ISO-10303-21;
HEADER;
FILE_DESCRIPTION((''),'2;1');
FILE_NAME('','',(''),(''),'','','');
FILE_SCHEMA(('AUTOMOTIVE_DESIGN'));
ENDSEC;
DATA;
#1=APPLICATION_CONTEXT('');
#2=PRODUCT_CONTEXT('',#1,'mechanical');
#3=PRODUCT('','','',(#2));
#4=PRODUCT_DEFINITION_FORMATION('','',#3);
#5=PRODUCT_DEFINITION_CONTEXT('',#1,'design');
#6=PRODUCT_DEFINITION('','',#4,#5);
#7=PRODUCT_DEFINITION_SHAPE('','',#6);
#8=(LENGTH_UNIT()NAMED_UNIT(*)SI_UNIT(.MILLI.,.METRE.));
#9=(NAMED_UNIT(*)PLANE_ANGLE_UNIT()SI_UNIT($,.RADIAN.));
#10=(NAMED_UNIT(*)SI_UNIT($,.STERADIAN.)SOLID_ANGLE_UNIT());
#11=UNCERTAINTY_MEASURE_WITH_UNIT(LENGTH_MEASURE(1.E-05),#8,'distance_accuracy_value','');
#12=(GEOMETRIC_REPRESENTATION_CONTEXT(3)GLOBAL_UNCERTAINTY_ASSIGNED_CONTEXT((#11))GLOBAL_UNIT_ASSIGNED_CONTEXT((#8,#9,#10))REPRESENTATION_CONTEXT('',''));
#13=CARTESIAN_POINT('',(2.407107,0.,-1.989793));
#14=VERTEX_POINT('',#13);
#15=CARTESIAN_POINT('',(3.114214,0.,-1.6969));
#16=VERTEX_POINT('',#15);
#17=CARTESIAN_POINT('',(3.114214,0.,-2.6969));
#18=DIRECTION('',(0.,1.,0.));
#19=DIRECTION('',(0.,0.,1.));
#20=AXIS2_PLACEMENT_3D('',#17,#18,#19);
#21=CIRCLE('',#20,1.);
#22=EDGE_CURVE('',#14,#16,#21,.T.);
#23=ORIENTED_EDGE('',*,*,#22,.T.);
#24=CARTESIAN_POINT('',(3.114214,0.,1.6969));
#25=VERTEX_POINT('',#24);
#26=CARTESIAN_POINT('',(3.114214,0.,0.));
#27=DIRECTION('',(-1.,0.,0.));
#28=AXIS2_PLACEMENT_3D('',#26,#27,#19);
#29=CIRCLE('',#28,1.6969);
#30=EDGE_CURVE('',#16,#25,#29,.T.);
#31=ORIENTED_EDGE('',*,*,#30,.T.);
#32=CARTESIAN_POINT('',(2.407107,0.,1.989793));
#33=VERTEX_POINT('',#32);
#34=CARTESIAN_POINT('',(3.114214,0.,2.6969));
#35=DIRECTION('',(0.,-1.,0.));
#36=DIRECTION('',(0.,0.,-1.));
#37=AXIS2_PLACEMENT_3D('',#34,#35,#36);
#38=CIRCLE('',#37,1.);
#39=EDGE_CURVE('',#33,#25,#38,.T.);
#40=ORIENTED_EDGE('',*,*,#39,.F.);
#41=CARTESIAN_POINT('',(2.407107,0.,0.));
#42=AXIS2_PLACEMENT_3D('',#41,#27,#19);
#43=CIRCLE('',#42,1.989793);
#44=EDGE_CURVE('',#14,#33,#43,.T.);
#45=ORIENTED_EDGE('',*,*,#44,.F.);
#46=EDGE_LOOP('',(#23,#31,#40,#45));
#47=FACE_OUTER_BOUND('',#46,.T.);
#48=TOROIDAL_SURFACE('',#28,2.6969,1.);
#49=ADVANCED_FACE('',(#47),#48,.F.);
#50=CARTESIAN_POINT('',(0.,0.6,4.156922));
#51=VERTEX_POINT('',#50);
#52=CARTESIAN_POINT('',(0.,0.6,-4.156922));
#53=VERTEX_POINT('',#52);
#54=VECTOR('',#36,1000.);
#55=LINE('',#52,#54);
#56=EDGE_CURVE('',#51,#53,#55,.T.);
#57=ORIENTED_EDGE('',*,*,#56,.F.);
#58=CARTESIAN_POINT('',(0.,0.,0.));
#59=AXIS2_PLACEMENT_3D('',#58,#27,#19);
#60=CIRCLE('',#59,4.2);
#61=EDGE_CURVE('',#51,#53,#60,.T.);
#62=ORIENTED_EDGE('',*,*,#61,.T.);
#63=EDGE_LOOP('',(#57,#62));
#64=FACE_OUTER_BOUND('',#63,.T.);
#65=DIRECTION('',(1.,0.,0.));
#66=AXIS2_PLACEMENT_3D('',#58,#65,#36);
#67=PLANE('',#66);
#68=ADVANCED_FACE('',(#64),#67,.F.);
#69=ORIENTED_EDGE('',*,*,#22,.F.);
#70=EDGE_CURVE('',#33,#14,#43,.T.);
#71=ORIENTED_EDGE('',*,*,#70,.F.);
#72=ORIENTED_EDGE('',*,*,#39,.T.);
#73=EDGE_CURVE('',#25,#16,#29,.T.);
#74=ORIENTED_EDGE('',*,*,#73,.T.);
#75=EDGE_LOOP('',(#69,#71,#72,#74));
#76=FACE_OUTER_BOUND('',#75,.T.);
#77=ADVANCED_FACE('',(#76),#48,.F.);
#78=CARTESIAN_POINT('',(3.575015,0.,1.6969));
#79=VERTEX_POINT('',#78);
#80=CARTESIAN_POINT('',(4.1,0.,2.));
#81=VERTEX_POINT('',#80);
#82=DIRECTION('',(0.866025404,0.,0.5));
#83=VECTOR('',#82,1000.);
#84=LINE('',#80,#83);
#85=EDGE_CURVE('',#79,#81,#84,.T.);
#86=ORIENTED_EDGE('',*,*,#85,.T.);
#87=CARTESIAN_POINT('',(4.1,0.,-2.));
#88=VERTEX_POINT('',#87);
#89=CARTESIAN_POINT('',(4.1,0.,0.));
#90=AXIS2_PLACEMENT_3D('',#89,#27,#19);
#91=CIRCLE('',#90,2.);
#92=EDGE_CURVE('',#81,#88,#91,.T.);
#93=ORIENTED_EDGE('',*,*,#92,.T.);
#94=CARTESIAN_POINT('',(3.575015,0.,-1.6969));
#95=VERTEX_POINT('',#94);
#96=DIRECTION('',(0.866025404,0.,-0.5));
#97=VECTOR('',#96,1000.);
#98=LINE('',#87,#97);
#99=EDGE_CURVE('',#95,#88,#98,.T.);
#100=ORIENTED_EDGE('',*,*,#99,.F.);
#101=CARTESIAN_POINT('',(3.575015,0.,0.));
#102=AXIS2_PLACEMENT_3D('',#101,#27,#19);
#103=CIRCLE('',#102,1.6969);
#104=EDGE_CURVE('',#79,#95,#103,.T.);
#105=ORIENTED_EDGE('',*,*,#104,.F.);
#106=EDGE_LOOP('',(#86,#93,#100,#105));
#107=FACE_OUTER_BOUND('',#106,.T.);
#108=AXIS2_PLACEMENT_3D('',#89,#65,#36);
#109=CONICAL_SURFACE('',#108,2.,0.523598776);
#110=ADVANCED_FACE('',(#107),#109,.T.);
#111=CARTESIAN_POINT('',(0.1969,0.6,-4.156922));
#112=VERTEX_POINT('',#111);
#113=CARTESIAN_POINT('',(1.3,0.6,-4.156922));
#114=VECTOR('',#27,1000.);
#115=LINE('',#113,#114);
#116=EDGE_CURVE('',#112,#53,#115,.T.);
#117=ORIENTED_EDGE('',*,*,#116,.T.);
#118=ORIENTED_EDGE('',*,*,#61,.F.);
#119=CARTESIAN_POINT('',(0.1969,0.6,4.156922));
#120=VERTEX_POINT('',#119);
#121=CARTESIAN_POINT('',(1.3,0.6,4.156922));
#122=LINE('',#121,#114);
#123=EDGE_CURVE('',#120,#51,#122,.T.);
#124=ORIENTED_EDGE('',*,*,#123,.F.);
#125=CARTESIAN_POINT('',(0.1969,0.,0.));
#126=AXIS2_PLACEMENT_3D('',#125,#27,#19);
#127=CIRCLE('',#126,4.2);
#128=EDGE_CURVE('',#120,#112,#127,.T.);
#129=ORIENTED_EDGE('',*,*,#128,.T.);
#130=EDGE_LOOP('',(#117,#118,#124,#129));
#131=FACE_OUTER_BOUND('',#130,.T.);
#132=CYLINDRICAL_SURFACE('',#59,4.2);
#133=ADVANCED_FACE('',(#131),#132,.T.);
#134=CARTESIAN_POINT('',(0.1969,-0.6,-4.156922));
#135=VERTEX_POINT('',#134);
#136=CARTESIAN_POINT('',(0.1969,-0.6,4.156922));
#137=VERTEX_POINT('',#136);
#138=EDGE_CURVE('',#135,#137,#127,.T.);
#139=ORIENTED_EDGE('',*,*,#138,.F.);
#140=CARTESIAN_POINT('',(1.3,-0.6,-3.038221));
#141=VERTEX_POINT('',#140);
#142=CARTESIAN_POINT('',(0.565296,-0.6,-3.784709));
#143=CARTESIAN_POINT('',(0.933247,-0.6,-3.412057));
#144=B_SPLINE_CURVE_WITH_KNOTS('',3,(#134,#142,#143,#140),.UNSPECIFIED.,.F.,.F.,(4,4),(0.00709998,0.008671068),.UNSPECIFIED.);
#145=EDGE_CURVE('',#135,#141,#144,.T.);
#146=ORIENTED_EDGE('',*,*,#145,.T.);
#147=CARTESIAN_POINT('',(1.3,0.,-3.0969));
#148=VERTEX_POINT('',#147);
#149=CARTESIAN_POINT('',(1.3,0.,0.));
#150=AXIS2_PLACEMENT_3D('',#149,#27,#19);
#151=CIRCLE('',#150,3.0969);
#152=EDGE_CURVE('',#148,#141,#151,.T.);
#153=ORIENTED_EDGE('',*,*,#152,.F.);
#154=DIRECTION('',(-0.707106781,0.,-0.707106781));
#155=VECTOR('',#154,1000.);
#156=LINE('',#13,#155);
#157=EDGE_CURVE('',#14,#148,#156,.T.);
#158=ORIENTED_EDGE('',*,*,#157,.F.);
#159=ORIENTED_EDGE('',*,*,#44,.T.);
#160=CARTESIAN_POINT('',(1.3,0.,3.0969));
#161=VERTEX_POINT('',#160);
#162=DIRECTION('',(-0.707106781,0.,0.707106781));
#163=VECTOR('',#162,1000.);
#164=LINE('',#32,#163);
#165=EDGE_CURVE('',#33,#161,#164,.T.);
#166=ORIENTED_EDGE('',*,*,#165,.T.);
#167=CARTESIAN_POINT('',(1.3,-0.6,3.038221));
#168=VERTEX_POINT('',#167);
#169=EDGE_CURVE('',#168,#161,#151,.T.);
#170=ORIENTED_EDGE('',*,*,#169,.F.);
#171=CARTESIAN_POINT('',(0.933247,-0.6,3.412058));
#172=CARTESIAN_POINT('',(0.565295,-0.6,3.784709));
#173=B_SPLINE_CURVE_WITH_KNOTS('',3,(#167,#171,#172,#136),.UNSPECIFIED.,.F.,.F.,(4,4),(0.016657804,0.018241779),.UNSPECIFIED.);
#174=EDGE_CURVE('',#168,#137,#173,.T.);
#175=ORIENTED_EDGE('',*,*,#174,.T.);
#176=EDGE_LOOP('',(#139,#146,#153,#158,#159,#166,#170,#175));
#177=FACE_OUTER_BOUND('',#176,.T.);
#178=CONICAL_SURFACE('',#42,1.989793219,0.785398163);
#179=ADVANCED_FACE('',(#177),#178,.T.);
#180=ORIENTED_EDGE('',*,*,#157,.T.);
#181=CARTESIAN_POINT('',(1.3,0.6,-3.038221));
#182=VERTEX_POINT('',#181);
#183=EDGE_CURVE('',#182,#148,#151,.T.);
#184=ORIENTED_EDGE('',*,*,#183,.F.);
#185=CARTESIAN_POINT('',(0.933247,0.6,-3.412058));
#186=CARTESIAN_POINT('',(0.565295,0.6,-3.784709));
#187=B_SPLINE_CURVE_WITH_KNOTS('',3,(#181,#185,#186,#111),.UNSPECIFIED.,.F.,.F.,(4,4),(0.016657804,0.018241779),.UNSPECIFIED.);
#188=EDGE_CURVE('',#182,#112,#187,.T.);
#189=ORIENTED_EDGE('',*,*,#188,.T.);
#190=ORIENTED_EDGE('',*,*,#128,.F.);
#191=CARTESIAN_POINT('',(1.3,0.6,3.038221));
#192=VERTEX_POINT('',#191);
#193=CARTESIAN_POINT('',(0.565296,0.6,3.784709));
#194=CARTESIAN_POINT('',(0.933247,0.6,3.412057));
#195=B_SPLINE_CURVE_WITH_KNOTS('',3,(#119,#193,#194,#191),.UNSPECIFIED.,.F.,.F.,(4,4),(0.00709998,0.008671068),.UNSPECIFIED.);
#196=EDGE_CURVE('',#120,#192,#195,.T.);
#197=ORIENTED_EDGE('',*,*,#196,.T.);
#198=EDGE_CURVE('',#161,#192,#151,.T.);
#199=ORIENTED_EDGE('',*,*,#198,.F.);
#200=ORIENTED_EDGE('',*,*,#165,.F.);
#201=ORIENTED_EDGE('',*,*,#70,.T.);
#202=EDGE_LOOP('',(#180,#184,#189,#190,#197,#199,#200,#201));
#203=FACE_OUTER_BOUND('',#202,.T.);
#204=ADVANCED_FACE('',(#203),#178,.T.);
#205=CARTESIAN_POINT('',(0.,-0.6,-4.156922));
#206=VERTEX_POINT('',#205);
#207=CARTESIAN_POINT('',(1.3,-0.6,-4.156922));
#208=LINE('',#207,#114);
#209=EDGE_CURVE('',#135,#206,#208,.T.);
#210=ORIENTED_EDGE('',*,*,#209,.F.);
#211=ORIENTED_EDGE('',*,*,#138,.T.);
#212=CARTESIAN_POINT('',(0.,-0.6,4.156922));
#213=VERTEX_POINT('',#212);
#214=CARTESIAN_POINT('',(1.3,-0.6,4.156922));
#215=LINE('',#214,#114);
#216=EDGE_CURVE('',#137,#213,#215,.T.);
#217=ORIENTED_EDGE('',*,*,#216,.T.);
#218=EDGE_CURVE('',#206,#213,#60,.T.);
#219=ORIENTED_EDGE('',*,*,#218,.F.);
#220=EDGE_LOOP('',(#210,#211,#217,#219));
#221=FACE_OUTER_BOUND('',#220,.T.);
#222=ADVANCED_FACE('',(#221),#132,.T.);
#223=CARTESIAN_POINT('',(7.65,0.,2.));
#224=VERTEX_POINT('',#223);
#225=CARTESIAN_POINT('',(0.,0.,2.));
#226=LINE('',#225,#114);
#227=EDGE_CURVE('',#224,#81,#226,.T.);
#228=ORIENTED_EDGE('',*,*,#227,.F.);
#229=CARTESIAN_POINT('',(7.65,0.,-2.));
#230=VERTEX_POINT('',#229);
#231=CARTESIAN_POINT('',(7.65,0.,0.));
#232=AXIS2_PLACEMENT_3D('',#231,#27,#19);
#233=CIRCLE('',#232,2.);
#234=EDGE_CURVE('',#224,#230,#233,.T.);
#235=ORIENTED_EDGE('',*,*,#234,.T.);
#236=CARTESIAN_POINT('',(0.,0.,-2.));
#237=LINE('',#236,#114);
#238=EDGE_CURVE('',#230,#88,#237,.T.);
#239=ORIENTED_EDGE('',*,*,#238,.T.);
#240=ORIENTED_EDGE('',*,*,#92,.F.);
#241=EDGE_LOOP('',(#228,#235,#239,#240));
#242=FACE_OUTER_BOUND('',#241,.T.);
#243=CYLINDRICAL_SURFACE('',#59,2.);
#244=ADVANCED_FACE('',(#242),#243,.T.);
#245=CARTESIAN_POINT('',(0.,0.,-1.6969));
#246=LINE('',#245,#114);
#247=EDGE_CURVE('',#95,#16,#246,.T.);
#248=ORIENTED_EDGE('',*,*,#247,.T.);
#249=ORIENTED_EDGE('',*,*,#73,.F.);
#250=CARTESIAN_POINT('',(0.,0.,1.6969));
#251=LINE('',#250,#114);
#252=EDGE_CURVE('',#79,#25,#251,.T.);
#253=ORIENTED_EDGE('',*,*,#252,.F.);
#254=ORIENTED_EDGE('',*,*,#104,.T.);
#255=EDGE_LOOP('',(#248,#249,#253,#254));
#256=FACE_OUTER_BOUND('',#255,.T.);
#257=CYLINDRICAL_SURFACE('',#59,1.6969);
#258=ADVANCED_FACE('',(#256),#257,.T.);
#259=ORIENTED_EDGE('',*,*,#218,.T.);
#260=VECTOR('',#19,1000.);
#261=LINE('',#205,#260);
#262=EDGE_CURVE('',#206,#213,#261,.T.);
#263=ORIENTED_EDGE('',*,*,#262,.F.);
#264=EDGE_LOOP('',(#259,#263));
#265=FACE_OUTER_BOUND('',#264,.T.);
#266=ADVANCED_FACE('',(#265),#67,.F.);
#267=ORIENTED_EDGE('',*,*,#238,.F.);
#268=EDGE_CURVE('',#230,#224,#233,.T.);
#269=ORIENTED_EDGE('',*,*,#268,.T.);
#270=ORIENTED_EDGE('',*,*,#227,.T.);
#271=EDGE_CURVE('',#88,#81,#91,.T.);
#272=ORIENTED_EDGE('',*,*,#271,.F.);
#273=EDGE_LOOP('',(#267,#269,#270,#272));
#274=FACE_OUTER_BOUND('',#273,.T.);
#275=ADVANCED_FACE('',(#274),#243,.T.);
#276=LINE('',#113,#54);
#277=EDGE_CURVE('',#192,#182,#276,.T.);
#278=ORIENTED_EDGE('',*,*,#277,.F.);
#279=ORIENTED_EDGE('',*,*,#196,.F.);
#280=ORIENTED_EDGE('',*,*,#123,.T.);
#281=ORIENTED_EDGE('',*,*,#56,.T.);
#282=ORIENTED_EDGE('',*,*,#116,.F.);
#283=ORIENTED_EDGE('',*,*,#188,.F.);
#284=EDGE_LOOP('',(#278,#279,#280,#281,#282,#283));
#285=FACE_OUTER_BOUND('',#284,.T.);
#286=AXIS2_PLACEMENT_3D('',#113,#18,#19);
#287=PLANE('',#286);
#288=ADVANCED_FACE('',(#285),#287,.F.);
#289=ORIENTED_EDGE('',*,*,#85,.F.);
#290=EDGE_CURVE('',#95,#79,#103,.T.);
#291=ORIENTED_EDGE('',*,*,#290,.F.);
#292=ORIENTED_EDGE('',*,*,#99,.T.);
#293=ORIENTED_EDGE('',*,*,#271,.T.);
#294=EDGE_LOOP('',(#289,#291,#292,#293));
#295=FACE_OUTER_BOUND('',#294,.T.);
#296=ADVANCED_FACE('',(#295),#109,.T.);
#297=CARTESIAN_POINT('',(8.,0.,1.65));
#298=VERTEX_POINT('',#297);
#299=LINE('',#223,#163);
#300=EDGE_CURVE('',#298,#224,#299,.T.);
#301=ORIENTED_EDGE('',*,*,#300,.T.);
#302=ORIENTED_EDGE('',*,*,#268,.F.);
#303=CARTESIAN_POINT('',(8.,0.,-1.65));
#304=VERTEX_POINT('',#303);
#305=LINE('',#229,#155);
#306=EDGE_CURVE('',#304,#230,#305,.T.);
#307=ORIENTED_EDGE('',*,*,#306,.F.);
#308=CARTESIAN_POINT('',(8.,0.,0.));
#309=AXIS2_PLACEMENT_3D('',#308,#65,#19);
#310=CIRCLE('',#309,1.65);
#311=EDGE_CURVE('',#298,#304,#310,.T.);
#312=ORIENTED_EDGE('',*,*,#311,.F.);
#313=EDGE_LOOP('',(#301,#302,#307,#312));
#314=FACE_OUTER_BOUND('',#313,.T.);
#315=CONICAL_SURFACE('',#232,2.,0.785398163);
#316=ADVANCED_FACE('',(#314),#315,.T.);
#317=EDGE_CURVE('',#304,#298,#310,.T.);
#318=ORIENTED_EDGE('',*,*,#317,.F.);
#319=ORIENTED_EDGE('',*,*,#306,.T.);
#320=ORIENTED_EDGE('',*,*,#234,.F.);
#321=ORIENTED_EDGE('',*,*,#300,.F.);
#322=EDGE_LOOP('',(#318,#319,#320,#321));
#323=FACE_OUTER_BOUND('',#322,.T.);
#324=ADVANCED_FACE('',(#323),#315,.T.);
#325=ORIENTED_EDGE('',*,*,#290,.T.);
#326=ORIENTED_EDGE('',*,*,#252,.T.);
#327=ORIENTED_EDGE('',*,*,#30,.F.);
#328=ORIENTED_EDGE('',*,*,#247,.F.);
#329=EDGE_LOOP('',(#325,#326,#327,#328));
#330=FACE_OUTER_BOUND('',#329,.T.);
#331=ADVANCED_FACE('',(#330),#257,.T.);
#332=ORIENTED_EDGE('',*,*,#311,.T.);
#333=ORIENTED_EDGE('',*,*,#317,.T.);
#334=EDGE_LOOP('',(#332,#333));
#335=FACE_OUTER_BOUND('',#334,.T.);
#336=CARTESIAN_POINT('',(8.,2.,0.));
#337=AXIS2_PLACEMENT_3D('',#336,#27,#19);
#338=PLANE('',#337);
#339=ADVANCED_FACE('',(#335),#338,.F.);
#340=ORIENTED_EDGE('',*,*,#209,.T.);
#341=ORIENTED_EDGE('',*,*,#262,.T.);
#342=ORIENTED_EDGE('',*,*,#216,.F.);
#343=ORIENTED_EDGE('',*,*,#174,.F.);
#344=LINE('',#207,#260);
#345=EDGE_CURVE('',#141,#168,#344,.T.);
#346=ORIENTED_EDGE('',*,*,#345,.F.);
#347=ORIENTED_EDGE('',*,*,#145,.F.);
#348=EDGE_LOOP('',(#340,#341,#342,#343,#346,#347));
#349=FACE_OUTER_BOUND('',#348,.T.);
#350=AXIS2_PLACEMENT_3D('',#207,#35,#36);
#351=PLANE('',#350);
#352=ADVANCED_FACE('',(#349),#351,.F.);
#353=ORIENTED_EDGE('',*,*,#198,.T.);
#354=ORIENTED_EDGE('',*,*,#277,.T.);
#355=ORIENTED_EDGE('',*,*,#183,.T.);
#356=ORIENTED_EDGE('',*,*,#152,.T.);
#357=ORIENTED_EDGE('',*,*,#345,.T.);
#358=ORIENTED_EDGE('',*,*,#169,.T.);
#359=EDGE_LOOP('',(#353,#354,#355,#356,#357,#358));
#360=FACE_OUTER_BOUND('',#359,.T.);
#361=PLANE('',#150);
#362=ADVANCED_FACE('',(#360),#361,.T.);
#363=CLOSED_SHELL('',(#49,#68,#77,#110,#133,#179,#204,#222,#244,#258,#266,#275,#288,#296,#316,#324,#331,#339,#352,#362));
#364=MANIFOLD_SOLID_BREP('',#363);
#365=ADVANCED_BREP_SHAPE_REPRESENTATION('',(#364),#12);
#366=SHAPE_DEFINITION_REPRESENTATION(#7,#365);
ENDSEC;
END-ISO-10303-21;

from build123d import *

# Parameters (mm, degrees)
CHAMFER1_SIZE      = 0.35
CUT_EXTRUDE1_START = -1.3
CUT_EXTRUDE1_DEPTH = 1.3


with BuildPart() as part:
    # Sketch1 → Base-Revolve (revolve)
    with BuildSketch(Plane.XY, mode=Mode.PRIVATE) as base_revolve_sk:
        with BuildLine():
            Line((0, 0), (0, 4.2))
            Line((0, 4.2), (0.1969, 4.2))
            Line((0.1969, 4.2), (2.407106781, 1.989793219))
            ThreePointArc((2.407106781, 1.989793219), (2.73153013, 1.773020467), (3.114213562, 1.6969))
            Line((3.114213562, 1.6969), (3.5750154, 1.6969))
            Line((3.5750154, 1.6969), (4.1, 2))
            Line((4.1, 2), (8, 2))
            Line((8, 2), (8, 0))
            Line((8, 0), (0, 0))
        make_face()
    revolve(base_revolve_sk.sketch.rotate(Axis((0, 0, 0), (1, 0, 0)), 90), axis=Axis((0, 0, 0), (1, 0, 0)))

    # Chamfer1
    chamfer1_edges = [part.edges().sort_by_distance(p)[0] for p in [
        (8, 0, -2),
    ]]
    chamfer(chamfer1_edges, length=CHAMFER1_SIZE)

    # Sketch3 → Cut-Extrude1 (cut)
    with BuildSketch(Plane.ZY.offset(CUT_EXTRUDE1_START)):
        with BuildLine():
            Line((-4.156921938, 0.6), (4.156921938, 0.6))
            ThreePointArc((4.156921938, 0.6), (4.2, 0), (4.156921938, -0.6))
            Line((4.156921938, -0.6), (-4.156921938, -0.6))
            ThreePointArc((-4.156921938, -0.6), (-4.2, 0), (-4.156921938, 0.6))
        make_face()
    extrude(amount=CUT_EXTRUDE1_DEPTH, mode=Mode.SUBTRACT)


solid = part.part
